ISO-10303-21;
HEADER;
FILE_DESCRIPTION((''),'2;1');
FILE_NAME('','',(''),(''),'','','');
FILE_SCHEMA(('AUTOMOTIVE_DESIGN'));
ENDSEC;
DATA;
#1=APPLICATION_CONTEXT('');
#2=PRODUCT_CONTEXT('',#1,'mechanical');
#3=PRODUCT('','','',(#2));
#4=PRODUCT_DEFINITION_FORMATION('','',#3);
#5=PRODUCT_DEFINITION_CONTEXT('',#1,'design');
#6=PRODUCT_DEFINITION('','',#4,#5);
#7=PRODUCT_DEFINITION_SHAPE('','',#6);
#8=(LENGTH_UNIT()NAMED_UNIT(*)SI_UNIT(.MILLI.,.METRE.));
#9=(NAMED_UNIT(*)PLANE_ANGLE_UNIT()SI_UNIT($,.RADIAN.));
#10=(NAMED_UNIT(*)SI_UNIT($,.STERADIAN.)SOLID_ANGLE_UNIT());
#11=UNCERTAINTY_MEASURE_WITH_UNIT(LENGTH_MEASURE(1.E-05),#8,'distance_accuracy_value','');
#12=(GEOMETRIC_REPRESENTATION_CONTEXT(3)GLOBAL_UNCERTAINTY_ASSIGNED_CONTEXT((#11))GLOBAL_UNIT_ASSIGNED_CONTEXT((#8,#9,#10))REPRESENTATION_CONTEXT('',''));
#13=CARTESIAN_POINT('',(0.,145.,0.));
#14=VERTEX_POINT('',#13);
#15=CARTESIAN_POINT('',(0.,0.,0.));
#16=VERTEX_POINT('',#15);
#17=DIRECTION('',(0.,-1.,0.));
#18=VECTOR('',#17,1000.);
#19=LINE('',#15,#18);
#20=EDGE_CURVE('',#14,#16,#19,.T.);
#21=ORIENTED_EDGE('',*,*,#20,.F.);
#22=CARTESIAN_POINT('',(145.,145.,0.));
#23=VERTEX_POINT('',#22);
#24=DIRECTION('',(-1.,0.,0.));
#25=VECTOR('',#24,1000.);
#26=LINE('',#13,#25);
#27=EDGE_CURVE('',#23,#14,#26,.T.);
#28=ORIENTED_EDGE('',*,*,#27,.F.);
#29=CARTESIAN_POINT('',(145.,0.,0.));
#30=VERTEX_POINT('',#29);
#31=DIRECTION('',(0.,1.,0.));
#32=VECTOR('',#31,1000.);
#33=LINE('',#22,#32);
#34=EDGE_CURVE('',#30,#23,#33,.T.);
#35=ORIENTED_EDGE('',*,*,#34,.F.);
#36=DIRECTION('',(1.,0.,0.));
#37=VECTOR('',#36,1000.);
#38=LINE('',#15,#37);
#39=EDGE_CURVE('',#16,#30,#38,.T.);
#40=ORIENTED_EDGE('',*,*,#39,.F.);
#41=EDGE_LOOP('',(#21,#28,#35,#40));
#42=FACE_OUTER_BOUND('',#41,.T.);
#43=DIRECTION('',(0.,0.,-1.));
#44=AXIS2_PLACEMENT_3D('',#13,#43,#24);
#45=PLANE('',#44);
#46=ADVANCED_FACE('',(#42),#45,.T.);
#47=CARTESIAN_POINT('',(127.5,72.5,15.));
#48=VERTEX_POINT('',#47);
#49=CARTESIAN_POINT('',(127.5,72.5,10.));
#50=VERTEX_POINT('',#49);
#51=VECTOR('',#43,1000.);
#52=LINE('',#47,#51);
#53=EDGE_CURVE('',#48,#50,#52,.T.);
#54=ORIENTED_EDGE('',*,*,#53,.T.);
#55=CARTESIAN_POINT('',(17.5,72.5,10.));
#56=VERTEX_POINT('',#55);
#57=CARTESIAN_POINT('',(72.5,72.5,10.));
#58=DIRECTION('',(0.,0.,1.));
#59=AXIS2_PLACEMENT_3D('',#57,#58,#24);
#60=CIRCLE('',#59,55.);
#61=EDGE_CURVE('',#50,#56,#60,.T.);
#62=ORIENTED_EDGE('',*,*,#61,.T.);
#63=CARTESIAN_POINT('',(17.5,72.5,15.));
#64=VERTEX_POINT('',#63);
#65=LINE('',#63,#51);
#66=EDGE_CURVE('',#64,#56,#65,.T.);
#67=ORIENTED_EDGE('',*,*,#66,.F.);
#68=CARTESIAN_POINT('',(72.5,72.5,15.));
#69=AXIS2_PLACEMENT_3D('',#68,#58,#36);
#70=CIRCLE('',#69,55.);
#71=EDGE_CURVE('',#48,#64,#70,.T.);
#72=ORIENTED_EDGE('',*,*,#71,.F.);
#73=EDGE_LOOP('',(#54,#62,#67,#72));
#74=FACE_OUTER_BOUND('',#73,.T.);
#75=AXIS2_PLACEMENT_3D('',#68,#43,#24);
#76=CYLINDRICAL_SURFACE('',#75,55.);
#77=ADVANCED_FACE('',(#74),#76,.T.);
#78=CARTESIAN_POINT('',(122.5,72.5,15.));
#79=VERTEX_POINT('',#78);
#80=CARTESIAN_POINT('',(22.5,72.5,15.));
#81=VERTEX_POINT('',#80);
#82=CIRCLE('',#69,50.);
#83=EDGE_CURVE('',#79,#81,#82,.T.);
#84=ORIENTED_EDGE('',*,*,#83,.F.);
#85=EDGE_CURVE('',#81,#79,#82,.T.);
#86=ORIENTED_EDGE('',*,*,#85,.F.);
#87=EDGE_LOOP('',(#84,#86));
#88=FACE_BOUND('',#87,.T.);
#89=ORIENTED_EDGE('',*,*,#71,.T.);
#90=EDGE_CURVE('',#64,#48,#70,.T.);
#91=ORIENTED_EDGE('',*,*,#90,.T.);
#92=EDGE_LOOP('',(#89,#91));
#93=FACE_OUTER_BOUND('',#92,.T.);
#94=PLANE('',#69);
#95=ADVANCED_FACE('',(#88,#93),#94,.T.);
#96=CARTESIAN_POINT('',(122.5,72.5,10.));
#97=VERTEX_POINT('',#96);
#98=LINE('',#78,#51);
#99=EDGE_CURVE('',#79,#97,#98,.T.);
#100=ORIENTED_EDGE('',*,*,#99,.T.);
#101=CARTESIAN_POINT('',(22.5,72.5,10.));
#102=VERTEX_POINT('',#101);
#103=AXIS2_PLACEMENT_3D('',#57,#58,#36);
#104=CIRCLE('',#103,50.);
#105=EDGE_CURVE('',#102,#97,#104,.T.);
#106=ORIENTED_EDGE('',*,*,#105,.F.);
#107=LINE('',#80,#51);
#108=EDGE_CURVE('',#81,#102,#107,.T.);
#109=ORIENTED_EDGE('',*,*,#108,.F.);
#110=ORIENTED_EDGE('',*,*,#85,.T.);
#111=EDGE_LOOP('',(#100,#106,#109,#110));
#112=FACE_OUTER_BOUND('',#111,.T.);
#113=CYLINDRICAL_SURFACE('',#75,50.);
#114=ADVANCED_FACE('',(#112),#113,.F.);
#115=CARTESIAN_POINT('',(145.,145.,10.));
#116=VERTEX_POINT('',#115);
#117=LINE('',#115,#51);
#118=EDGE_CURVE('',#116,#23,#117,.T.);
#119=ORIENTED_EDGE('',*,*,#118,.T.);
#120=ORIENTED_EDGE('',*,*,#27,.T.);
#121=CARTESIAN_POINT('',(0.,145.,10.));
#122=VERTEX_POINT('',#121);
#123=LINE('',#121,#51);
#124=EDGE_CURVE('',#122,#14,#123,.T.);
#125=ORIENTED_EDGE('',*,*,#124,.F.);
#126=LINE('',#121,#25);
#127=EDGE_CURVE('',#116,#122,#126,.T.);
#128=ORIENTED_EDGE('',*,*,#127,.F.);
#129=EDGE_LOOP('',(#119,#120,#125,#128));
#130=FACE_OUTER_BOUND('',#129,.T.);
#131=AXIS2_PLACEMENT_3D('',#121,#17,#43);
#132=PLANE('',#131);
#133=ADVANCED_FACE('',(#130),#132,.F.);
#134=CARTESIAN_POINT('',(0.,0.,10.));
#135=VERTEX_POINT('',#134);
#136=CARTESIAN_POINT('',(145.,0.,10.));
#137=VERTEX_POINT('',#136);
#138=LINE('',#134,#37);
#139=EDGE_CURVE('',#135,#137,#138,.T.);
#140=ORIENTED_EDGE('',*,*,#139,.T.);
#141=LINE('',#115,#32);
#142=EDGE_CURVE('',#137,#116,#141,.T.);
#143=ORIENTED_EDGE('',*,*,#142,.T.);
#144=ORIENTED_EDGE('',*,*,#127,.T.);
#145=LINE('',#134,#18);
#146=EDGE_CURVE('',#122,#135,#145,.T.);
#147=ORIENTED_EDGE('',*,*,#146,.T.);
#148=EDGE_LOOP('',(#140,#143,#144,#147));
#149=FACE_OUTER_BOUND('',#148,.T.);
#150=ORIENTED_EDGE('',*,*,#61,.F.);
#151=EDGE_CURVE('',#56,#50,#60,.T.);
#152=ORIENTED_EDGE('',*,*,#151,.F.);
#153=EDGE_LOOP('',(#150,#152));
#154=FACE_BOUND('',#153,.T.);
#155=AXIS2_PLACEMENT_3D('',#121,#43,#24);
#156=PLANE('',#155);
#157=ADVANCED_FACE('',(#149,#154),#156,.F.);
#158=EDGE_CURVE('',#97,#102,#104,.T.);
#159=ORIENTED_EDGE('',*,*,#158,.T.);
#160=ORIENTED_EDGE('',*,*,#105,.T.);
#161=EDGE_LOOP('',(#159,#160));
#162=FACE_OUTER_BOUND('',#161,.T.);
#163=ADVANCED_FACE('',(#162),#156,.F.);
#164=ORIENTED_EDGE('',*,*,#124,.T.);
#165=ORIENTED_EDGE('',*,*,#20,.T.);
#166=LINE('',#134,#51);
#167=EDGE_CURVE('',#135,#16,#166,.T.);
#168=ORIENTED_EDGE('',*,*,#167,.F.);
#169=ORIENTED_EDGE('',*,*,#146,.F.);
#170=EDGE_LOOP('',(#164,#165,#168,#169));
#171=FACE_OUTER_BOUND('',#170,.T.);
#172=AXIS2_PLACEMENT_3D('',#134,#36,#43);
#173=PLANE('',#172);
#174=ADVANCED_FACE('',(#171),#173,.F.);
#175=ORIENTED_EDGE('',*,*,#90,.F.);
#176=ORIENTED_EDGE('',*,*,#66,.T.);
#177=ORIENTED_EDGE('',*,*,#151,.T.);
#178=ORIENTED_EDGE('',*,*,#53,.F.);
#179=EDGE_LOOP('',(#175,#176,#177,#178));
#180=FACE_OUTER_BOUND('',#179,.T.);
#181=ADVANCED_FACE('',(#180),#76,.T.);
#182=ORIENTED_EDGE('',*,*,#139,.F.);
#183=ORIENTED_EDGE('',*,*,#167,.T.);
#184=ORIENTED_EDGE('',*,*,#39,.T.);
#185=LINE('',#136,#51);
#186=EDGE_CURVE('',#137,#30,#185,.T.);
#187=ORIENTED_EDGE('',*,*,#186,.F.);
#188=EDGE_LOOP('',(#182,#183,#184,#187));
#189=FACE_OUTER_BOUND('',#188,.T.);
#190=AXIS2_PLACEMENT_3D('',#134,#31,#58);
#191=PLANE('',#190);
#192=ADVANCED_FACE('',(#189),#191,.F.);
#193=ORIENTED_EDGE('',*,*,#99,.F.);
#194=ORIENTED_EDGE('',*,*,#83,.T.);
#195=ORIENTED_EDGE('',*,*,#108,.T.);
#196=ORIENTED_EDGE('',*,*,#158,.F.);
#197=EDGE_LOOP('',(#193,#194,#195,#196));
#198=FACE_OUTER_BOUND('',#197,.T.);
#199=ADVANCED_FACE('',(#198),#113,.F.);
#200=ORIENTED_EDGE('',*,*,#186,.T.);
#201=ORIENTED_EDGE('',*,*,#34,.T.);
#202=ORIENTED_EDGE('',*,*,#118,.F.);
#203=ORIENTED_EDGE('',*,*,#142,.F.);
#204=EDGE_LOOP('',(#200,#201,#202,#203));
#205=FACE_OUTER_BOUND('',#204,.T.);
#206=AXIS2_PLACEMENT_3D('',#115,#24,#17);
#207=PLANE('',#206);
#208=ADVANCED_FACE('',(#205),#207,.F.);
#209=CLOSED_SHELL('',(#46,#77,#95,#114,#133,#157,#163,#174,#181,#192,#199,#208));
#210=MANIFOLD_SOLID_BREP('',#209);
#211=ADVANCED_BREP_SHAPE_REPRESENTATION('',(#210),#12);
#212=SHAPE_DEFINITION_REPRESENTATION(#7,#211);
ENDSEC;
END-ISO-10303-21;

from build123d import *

# Parameters (mm, degrees)
SKETCH1_W           = 145
SKETCH1_H           = 145
BOSS_EXTRUDE1_DEPTH = 10
SKETCH2_R           = 55
SKETCH2_R_2         = 50
BOSS_EXTRUDE2_DEPTH = 5


with BuildPart() as part:
    # Sketch1 → Boss-Extrude1 (new body)
    with BuildSketch(Plane.XY):
        with Locations((72.5, 72.5)):
            Rectangle(SKETCH1_W, SKETCH1_H)
    extrude(amount=BOSS_EXTRUDE1_DEPTH)

    # Sketch2 → Boss-Extrude2 (add)
    with BuildSketch(Plane.XY.offset(10)):
        with Locations(Location((72.5, 72.5, 0), (0, 0, 180))):
            Circle(SKETCH2_R)
        with Locations((72.5, 72.5)):
            Circle(SKETCH2_R_2, mode=Mode.SUBTRACT)
    extrude(amount=BOSS_EXTRUDE2_DEPTH)


solid = part.part
